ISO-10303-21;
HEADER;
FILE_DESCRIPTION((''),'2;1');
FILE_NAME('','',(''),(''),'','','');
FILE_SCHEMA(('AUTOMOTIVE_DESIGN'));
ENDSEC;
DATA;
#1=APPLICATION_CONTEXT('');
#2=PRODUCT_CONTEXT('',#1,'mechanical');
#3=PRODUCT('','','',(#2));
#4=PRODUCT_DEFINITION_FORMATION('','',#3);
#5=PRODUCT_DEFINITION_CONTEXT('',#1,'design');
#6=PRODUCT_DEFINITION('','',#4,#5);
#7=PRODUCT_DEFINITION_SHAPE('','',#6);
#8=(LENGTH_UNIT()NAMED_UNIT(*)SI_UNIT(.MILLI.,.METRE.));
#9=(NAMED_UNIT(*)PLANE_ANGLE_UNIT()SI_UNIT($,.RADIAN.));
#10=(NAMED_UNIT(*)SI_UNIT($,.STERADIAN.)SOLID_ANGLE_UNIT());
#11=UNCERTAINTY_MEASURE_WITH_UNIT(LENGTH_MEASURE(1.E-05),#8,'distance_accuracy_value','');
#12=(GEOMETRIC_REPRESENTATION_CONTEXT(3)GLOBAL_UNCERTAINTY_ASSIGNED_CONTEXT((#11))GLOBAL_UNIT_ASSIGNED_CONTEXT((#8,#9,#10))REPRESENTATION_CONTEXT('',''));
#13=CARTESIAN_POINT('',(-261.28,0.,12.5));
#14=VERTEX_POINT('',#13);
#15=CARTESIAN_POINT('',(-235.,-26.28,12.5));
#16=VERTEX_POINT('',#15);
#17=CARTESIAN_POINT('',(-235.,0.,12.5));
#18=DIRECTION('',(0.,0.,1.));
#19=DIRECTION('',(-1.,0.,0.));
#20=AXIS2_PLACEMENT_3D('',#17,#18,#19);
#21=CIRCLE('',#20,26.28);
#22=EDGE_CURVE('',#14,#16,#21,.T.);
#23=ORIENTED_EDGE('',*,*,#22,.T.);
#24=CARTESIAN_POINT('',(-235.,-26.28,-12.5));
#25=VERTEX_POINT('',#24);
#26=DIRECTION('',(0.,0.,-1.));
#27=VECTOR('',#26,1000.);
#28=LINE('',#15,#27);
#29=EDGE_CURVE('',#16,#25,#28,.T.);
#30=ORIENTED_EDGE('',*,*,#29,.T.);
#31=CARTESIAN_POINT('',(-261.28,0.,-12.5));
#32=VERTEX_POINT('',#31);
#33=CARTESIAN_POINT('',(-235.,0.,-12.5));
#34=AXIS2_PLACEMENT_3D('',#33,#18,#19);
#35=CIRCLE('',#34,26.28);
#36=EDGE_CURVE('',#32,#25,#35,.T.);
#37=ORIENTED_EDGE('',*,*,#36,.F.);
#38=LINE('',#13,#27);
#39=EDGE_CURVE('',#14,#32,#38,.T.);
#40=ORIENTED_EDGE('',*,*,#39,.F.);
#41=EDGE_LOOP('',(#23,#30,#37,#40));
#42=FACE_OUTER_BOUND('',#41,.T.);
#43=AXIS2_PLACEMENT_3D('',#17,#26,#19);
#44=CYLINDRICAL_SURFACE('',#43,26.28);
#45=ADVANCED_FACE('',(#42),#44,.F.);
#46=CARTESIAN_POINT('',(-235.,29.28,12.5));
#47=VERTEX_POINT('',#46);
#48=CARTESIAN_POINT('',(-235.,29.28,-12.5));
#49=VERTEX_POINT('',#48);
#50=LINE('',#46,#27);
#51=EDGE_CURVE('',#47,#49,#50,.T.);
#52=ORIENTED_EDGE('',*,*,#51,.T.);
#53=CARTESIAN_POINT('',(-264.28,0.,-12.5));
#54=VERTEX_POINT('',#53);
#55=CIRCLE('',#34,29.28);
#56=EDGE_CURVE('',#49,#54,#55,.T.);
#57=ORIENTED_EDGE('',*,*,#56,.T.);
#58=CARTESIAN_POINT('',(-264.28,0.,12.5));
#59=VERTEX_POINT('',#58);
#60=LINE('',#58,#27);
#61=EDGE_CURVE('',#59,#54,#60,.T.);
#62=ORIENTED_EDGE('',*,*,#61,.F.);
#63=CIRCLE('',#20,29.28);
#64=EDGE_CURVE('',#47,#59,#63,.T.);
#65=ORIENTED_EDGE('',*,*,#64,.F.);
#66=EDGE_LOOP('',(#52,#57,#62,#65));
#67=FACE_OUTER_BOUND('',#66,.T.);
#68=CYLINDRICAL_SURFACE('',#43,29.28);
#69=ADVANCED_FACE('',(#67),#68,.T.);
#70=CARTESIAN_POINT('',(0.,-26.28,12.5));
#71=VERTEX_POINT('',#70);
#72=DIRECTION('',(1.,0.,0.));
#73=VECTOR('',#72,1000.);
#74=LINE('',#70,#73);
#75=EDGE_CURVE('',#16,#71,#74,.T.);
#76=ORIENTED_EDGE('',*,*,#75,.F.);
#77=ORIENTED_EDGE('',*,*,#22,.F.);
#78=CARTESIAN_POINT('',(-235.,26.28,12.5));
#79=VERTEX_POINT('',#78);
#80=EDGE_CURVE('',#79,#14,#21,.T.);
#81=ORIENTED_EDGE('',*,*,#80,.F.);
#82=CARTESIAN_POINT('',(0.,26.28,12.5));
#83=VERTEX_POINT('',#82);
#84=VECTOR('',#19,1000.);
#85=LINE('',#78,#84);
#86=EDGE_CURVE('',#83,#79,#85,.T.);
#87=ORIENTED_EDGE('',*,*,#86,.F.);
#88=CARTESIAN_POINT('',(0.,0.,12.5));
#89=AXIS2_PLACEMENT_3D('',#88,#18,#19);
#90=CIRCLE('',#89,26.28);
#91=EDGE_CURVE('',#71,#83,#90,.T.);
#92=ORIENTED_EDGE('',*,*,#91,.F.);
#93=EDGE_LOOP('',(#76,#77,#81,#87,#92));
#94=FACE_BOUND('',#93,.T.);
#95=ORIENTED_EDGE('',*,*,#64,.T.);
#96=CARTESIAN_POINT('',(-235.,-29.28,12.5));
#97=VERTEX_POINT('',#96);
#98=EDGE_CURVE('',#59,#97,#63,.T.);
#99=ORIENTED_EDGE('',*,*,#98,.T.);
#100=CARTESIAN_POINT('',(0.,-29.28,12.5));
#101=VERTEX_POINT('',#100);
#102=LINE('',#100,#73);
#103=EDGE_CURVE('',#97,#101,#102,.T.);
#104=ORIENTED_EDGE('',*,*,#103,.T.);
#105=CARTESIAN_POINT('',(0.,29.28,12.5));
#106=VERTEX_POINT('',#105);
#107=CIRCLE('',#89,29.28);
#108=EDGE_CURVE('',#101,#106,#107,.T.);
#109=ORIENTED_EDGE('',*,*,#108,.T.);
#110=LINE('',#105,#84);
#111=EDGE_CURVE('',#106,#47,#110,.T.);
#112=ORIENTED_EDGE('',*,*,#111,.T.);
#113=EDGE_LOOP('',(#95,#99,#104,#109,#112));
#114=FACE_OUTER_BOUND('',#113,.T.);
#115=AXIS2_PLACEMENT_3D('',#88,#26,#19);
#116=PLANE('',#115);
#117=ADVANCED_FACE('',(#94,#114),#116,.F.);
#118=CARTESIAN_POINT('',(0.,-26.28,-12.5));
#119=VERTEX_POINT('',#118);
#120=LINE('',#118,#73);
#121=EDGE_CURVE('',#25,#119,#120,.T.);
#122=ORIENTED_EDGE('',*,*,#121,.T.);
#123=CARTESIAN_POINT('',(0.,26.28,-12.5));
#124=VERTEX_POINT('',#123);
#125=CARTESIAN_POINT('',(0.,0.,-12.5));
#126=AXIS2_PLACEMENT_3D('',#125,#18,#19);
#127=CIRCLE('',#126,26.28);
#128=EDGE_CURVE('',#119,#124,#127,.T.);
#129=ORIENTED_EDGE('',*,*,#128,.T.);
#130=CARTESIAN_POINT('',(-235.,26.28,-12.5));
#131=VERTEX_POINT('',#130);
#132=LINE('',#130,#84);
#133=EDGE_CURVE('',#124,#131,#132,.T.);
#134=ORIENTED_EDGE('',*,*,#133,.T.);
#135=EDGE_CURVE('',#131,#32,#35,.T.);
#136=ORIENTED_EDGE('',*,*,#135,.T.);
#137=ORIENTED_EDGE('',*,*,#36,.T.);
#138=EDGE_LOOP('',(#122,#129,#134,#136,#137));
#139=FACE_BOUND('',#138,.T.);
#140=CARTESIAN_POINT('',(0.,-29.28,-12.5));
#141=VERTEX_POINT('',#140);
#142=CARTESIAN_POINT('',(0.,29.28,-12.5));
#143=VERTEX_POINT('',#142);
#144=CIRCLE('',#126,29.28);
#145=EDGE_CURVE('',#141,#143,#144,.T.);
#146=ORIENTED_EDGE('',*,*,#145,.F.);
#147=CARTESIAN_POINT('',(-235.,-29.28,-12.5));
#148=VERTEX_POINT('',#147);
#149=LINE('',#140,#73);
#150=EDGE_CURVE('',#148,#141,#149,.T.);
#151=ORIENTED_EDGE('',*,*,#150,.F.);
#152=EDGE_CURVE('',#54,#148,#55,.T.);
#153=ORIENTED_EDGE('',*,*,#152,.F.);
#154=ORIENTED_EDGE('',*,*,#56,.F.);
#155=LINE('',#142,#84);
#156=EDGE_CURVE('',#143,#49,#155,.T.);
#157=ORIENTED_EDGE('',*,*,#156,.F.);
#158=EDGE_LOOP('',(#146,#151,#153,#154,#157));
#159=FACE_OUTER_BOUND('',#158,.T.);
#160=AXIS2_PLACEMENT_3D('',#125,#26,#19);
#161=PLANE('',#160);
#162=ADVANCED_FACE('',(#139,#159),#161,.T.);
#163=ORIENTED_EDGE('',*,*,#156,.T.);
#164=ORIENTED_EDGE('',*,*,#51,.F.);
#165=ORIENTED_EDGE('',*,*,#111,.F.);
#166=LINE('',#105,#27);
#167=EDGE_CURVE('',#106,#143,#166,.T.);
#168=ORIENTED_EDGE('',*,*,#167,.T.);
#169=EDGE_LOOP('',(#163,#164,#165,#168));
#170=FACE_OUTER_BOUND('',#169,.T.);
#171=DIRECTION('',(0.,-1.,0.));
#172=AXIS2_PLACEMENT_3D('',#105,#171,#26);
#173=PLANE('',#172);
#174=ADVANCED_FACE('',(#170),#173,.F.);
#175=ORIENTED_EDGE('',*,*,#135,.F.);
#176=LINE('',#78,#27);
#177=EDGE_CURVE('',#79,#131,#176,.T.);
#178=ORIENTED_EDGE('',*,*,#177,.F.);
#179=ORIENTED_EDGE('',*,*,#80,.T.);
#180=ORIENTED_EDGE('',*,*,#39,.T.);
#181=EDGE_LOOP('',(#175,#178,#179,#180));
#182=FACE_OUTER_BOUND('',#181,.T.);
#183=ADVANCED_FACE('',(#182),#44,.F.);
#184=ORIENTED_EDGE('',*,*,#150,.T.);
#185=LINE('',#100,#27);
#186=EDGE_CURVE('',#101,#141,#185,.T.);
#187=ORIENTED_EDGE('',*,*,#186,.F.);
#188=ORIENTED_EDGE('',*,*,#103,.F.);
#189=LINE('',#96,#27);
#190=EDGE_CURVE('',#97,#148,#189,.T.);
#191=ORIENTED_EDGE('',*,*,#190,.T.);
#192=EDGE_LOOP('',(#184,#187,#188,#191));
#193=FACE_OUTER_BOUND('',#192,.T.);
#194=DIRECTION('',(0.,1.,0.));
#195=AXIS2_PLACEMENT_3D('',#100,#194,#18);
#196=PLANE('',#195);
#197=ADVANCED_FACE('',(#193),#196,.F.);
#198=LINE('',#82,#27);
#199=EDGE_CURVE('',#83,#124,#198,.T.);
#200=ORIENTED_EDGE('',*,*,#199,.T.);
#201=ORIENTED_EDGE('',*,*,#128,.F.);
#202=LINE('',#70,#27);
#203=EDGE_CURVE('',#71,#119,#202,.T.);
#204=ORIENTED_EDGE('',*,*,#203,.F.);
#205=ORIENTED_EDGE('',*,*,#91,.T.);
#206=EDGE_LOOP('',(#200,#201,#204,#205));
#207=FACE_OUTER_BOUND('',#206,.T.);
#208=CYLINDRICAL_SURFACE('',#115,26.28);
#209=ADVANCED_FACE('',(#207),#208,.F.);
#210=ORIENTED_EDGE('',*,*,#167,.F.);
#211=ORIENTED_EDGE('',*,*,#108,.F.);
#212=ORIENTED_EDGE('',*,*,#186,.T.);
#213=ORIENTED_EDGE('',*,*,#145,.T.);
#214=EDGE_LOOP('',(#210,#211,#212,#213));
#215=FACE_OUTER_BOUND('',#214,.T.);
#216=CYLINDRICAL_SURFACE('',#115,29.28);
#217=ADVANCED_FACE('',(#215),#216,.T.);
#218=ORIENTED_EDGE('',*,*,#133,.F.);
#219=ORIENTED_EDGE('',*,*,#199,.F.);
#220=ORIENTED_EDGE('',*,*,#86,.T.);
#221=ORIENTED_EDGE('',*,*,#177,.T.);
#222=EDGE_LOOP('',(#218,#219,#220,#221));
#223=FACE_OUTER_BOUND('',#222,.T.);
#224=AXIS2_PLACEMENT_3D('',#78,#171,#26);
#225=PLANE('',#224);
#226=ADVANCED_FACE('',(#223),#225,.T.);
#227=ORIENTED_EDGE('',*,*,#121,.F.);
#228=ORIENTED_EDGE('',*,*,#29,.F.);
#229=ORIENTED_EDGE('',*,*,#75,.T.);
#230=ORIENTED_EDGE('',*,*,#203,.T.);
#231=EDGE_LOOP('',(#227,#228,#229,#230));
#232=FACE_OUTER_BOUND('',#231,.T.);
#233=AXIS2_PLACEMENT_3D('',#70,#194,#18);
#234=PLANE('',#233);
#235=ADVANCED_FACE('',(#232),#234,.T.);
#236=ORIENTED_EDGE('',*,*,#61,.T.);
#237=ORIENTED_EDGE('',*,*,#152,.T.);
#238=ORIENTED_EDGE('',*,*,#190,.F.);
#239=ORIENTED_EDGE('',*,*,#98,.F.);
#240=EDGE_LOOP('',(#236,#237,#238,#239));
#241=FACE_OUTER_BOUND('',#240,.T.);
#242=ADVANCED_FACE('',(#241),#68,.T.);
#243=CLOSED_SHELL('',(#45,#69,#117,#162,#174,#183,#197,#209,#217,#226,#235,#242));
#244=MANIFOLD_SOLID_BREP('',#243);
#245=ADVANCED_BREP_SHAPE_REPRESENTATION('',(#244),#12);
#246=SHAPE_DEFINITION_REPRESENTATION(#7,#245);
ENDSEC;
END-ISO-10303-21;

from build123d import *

# Parameters (mm, degrees)
EXTRUDE_THIN1_DEPTH = 12.5


with BuildPart() as part:
    # Sketch2 → Extrude-Thin1 (new, symmetric)
    with BuildSketch(Plane.XY):
        with BuildLine():
            Line((-235, 29.28), (0, 29.28))
            ThreePointArc((0, 29.28), (29.28, 0), (0, -29.28))
            Line((0, -29.28), (-235, -29.28))
            ThreePointArc((-235, -29.28), (-264.28, 0), (-235, 29.28))
        make_face()
        with BuildLine():
            Line((-235, 26.28), (0, 26.28))
            ThreePointArc((0, 26.28), (26.28, 0), (0, -26.28))
            Line((0, -26.28), (-235, -26.28))
            ThreePointArc((-235, -26.28), (-261.28, 0), (-235, 26.28))
        make_face(mode=Mode.SUBTRACT)
    extrude(amount=EXTRUDE_THIN1_DEPTH, both=True)


solid = part.part
